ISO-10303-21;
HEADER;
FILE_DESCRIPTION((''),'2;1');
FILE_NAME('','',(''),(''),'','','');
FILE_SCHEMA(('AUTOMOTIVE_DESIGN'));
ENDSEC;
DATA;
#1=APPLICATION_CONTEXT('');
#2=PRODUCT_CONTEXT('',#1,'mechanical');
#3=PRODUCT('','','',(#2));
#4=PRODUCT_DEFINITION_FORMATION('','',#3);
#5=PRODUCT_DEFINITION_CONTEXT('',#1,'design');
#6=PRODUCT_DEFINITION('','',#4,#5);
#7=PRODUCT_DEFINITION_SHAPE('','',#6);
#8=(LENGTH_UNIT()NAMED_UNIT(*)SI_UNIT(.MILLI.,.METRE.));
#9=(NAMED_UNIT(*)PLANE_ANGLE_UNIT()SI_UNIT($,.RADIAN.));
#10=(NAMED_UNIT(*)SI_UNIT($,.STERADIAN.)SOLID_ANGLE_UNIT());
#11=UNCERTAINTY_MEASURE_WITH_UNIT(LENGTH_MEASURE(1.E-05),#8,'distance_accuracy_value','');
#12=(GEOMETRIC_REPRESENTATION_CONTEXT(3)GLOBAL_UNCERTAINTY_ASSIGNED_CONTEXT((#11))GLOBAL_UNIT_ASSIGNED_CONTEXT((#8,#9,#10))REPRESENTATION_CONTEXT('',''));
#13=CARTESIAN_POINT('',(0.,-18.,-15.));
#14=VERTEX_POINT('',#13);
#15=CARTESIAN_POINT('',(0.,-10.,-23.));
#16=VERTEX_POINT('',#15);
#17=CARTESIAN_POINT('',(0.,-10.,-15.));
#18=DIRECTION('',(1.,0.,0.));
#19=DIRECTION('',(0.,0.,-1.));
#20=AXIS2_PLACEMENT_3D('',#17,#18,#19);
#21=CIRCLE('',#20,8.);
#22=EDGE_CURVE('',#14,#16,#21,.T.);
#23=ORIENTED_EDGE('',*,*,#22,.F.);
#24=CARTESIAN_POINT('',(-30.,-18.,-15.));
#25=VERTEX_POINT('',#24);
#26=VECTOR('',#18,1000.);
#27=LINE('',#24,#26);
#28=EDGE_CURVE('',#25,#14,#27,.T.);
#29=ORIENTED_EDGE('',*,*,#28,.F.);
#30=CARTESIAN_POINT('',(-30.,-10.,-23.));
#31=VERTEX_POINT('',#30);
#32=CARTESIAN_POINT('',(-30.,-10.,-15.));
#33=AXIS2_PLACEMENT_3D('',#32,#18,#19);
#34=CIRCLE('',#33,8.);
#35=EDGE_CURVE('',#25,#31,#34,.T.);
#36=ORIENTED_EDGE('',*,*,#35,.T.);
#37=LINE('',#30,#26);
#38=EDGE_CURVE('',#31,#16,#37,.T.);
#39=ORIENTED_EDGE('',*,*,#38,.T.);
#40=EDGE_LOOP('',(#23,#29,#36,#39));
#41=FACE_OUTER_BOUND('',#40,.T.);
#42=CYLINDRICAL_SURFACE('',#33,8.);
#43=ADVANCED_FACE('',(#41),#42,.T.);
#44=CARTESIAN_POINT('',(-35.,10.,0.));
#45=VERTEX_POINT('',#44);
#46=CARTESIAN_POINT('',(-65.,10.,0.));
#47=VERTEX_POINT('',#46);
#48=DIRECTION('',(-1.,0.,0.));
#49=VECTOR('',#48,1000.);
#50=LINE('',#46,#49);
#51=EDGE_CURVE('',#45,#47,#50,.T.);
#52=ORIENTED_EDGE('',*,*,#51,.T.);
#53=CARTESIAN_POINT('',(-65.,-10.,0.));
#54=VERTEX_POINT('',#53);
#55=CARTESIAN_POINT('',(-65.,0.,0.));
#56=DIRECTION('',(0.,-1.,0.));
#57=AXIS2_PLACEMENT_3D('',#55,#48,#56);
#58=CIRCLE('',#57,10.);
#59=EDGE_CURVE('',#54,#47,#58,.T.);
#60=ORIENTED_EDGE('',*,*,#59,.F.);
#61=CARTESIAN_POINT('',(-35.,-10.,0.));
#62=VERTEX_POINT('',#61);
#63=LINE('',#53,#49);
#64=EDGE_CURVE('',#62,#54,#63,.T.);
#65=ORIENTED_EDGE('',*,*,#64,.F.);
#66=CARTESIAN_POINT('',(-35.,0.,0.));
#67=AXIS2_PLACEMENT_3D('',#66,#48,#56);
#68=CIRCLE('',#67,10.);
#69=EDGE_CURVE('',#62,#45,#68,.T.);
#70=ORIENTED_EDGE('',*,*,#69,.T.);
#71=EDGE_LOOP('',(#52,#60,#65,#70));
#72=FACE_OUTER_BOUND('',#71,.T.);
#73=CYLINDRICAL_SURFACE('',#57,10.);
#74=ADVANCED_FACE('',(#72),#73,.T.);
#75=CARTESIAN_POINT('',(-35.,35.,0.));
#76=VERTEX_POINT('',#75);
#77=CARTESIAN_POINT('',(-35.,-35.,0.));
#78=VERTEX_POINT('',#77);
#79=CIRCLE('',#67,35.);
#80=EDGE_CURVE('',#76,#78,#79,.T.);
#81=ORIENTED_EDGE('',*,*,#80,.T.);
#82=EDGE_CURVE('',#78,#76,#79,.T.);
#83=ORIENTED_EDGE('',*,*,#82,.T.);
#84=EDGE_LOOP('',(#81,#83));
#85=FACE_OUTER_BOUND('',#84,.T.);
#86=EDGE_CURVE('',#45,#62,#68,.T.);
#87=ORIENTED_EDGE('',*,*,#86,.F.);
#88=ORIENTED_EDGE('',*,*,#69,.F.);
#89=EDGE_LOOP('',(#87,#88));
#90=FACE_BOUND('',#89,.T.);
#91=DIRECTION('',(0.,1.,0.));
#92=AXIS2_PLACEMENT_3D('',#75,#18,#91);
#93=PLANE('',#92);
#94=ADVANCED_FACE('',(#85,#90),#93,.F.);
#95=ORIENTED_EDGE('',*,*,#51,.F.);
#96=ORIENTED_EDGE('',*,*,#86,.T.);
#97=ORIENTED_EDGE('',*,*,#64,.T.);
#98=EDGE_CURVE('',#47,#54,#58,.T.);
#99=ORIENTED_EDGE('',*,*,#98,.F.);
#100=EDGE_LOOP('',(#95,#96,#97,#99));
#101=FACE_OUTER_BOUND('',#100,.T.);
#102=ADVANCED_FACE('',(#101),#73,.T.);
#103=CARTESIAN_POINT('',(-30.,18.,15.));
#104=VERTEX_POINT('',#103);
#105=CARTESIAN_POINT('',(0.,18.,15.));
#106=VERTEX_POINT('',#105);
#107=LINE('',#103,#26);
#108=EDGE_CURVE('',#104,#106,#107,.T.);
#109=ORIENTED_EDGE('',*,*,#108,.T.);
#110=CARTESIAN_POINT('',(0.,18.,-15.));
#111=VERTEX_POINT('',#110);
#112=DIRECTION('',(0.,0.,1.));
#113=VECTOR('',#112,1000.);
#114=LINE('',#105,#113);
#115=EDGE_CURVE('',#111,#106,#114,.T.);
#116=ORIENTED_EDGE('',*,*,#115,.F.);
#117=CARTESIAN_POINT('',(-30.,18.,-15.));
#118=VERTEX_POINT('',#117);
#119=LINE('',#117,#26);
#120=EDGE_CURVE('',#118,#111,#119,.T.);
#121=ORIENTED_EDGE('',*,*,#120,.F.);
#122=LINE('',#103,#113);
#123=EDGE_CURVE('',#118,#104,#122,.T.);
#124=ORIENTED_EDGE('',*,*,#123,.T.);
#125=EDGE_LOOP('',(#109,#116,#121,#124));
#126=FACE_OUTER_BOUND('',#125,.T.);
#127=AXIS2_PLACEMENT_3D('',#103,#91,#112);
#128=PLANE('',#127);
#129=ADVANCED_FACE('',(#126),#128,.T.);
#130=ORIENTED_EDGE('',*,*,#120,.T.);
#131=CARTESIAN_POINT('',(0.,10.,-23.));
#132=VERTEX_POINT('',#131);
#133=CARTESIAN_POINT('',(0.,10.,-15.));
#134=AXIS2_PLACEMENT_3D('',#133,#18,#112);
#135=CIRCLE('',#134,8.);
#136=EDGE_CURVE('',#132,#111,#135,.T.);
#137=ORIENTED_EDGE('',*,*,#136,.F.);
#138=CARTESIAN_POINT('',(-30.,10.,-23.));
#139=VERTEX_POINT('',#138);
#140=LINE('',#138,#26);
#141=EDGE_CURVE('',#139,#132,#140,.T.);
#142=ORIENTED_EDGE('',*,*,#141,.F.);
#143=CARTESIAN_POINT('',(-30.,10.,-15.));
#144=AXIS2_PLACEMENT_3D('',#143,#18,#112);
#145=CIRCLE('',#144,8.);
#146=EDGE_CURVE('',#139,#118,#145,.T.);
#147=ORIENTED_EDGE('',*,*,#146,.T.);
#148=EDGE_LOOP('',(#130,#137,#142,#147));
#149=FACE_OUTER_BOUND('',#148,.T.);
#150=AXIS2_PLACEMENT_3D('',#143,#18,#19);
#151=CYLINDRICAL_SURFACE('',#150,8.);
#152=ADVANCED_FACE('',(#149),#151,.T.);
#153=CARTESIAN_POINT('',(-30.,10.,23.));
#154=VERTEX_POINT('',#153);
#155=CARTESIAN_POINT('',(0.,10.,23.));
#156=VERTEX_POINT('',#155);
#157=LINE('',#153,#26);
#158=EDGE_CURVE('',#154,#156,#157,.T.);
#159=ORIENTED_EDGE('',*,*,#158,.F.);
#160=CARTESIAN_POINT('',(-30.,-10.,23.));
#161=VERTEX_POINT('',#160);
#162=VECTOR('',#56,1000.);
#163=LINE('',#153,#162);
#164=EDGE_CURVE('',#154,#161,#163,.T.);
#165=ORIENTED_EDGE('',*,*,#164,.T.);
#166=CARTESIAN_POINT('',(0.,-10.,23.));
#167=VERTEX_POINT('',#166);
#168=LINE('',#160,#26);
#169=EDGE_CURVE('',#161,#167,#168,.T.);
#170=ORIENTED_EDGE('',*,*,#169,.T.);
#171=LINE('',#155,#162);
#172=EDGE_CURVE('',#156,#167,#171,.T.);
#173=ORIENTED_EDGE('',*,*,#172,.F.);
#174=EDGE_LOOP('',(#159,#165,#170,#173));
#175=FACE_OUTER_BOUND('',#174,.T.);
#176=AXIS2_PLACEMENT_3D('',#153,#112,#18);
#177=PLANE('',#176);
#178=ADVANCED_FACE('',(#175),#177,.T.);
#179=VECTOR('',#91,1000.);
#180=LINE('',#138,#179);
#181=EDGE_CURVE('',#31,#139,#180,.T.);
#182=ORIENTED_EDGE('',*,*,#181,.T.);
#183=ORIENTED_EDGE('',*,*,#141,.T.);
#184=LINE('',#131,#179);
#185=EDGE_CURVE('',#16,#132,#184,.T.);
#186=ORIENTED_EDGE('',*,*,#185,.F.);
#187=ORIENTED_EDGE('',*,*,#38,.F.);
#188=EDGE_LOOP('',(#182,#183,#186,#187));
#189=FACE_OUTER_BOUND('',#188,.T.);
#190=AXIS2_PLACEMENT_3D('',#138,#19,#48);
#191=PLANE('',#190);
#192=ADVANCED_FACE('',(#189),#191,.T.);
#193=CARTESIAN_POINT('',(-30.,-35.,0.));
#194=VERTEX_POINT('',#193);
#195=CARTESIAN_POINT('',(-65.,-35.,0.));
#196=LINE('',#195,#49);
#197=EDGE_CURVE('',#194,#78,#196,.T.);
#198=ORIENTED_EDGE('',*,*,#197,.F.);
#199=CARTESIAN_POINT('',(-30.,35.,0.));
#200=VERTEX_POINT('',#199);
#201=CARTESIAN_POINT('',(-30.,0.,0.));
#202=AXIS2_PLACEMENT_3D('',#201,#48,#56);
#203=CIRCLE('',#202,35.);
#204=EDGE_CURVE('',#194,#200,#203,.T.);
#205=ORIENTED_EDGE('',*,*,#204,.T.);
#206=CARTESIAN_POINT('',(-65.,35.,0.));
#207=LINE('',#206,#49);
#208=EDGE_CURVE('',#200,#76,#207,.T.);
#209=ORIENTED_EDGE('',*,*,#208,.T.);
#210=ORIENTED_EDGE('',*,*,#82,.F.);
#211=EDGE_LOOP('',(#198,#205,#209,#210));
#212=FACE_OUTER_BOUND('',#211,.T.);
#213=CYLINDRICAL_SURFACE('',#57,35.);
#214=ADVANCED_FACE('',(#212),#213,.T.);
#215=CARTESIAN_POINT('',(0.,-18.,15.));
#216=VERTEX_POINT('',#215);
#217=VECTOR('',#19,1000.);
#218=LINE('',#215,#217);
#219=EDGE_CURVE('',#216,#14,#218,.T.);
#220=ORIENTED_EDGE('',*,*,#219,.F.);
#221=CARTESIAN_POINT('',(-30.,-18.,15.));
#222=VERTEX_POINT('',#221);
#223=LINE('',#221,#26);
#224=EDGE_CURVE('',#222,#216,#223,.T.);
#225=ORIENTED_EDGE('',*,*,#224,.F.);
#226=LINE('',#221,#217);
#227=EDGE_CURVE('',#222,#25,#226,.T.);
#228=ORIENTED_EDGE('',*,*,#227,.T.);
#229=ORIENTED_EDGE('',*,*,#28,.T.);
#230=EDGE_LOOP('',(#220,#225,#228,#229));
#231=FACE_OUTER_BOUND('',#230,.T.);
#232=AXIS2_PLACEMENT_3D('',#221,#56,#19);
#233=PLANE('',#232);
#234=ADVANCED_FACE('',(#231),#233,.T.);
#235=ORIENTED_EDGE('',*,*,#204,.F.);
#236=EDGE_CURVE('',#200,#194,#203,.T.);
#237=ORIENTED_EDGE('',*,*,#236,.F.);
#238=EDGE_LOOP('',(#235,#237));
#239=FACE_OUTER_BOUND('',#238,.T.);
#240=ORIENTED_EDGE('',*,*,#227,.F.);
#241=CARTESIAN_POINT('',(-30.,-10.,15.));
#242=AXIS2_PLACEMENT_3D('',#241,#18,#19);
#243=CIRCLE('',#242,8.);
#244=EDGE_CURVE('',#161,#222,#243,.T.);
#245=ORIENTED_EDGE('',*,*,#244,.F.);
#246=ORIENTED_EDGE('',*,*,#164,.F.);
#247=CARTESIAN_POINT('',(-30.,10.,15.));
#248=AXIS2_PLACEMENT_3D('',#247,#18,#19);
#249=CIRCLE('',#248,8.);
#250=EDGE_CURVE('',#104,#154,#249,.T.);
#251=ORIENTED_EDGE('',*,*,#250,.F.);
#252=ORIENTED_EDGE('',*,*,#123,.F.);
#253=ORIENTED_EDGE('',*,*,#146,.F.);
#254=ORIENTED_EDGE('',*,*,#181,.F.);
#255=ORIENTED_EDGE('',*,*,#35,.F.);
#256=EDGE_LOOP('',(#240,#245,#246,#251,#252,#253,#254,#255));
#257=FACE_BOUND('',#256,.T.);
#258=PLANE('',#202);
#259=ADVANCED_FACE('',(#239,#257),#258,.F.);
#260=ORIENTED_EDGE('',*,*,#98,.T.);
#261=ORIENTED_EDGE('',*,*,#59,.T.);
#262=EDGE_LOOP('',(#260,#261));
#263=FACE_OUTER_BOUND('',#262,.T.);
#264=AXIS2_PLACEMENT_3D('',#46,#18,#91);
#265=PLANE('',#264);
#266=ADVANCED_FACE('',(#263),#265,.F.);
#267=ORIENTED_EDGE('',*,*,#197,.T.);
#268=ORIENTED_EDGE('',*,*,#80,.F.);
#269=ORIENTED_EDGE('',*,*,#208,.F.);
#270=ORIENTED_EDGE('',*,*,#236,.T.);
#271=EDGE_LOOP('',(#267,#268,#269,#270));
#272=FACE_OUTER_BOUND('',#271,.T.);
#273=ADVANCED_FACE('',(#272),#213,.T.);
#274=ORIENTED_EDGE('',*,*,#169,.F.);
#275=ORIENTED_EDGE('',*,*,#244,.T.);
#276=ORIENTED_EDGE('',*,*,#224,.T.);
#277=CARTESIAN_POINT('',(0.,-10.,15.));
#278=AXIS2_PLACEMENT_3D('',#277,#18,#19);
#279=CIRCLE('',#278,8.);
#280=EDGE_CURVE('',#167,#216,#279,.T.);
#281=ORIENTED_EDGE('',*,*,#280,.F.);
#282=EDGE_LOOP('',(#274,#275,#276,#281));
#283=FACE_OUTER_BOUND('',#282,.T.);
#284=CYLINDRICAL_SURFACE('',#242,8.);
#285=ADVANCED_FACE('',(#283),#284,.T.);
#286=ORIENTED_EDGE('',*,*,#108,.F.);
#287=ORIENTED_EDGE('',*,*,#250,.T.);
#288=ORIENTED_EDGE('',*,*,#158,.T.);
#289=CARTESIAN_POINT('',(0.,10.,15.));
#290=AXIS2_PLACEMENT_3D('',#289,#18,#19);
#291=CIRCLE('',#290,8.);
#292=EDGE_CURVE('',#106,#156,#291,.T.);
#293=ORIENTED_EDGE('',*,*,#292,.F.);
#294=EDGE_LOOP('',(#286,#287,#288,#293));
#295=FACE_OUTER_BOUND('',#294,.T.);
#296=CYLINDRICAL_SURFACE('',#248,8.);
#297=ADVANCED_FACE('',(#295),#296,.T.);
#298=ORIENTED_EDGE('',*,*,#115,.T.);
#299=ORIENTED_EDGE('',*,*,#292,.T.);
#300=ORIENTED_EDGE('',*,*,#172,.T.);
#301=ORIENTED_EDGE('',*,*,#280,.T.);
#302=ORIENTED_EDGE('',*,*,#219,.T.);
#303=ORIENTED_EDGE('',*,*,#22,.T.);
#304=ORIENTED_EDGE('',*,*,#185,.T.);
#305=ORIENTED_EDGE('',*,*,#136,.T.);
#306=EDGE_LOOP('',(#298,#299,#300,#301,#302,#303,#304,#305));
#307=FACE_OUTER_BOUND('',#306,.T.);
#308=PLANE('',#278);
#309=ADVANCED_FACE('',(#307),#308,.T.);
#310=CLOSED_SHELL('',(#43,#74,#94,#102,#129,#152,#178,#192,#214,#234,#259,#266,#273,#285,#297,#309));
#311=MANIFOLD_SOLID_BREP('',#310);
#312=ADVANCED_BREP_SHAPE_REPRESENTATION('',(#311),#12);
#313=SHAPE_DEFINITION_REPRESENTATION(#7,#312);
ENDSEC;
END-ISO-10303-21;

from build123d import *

# Parameters (mm, degrees)
BOSS_EXTRUDE1_DEPTH = 30


with BuildPart() as part:
    # Sketch2 → Boss-Extrude1 (new body)
    with BuildSketch(Plane(origin=(0, 0, 0), x_dir=(0, 0, -1), z_dir=(1, 0, 0))):
        with BuildLine():
            Line((-15, 18), (15, 18))
            ThreePointArc((15, 18), (20.656854249, 15.656854249), (23, 10))
            Line((23, 10), (23, -10))
            ThreePointArc((23, -10), (20.656854249, -15.656854249), (15, -18))
            Line((15, -18), (-15, -18))
            ThreePointArc((-15, -18), (-20.656854249, -15.656854249), (-23, -10))
            Line((-23, -10), (-23, 10))
            ThreePointArc((-23, 10), (-20.656854249, 15.656854249), (-15, 18))
        make_face()
    extrude(amount=-BOSS_EXTRUDE1_DEPTH)

    # Sketch3 → Revolve1 (revolve)
    with BuildSketch(Plane.XY, mode=Mode.PRIVATE) as revolve1_sk:
        Polygon((-30, 0), (-30, 35), (-35, 35), (-35, 10), (-65, 10), (-65, 0), align=None)
    revolve(revolve1_sk.sketch.rotate(Axis((-65, 0, 0), (1, 0, 0)), 180), axis=Axis((-65, 0, 0), (1, 0, 0)))


solid = part.part
